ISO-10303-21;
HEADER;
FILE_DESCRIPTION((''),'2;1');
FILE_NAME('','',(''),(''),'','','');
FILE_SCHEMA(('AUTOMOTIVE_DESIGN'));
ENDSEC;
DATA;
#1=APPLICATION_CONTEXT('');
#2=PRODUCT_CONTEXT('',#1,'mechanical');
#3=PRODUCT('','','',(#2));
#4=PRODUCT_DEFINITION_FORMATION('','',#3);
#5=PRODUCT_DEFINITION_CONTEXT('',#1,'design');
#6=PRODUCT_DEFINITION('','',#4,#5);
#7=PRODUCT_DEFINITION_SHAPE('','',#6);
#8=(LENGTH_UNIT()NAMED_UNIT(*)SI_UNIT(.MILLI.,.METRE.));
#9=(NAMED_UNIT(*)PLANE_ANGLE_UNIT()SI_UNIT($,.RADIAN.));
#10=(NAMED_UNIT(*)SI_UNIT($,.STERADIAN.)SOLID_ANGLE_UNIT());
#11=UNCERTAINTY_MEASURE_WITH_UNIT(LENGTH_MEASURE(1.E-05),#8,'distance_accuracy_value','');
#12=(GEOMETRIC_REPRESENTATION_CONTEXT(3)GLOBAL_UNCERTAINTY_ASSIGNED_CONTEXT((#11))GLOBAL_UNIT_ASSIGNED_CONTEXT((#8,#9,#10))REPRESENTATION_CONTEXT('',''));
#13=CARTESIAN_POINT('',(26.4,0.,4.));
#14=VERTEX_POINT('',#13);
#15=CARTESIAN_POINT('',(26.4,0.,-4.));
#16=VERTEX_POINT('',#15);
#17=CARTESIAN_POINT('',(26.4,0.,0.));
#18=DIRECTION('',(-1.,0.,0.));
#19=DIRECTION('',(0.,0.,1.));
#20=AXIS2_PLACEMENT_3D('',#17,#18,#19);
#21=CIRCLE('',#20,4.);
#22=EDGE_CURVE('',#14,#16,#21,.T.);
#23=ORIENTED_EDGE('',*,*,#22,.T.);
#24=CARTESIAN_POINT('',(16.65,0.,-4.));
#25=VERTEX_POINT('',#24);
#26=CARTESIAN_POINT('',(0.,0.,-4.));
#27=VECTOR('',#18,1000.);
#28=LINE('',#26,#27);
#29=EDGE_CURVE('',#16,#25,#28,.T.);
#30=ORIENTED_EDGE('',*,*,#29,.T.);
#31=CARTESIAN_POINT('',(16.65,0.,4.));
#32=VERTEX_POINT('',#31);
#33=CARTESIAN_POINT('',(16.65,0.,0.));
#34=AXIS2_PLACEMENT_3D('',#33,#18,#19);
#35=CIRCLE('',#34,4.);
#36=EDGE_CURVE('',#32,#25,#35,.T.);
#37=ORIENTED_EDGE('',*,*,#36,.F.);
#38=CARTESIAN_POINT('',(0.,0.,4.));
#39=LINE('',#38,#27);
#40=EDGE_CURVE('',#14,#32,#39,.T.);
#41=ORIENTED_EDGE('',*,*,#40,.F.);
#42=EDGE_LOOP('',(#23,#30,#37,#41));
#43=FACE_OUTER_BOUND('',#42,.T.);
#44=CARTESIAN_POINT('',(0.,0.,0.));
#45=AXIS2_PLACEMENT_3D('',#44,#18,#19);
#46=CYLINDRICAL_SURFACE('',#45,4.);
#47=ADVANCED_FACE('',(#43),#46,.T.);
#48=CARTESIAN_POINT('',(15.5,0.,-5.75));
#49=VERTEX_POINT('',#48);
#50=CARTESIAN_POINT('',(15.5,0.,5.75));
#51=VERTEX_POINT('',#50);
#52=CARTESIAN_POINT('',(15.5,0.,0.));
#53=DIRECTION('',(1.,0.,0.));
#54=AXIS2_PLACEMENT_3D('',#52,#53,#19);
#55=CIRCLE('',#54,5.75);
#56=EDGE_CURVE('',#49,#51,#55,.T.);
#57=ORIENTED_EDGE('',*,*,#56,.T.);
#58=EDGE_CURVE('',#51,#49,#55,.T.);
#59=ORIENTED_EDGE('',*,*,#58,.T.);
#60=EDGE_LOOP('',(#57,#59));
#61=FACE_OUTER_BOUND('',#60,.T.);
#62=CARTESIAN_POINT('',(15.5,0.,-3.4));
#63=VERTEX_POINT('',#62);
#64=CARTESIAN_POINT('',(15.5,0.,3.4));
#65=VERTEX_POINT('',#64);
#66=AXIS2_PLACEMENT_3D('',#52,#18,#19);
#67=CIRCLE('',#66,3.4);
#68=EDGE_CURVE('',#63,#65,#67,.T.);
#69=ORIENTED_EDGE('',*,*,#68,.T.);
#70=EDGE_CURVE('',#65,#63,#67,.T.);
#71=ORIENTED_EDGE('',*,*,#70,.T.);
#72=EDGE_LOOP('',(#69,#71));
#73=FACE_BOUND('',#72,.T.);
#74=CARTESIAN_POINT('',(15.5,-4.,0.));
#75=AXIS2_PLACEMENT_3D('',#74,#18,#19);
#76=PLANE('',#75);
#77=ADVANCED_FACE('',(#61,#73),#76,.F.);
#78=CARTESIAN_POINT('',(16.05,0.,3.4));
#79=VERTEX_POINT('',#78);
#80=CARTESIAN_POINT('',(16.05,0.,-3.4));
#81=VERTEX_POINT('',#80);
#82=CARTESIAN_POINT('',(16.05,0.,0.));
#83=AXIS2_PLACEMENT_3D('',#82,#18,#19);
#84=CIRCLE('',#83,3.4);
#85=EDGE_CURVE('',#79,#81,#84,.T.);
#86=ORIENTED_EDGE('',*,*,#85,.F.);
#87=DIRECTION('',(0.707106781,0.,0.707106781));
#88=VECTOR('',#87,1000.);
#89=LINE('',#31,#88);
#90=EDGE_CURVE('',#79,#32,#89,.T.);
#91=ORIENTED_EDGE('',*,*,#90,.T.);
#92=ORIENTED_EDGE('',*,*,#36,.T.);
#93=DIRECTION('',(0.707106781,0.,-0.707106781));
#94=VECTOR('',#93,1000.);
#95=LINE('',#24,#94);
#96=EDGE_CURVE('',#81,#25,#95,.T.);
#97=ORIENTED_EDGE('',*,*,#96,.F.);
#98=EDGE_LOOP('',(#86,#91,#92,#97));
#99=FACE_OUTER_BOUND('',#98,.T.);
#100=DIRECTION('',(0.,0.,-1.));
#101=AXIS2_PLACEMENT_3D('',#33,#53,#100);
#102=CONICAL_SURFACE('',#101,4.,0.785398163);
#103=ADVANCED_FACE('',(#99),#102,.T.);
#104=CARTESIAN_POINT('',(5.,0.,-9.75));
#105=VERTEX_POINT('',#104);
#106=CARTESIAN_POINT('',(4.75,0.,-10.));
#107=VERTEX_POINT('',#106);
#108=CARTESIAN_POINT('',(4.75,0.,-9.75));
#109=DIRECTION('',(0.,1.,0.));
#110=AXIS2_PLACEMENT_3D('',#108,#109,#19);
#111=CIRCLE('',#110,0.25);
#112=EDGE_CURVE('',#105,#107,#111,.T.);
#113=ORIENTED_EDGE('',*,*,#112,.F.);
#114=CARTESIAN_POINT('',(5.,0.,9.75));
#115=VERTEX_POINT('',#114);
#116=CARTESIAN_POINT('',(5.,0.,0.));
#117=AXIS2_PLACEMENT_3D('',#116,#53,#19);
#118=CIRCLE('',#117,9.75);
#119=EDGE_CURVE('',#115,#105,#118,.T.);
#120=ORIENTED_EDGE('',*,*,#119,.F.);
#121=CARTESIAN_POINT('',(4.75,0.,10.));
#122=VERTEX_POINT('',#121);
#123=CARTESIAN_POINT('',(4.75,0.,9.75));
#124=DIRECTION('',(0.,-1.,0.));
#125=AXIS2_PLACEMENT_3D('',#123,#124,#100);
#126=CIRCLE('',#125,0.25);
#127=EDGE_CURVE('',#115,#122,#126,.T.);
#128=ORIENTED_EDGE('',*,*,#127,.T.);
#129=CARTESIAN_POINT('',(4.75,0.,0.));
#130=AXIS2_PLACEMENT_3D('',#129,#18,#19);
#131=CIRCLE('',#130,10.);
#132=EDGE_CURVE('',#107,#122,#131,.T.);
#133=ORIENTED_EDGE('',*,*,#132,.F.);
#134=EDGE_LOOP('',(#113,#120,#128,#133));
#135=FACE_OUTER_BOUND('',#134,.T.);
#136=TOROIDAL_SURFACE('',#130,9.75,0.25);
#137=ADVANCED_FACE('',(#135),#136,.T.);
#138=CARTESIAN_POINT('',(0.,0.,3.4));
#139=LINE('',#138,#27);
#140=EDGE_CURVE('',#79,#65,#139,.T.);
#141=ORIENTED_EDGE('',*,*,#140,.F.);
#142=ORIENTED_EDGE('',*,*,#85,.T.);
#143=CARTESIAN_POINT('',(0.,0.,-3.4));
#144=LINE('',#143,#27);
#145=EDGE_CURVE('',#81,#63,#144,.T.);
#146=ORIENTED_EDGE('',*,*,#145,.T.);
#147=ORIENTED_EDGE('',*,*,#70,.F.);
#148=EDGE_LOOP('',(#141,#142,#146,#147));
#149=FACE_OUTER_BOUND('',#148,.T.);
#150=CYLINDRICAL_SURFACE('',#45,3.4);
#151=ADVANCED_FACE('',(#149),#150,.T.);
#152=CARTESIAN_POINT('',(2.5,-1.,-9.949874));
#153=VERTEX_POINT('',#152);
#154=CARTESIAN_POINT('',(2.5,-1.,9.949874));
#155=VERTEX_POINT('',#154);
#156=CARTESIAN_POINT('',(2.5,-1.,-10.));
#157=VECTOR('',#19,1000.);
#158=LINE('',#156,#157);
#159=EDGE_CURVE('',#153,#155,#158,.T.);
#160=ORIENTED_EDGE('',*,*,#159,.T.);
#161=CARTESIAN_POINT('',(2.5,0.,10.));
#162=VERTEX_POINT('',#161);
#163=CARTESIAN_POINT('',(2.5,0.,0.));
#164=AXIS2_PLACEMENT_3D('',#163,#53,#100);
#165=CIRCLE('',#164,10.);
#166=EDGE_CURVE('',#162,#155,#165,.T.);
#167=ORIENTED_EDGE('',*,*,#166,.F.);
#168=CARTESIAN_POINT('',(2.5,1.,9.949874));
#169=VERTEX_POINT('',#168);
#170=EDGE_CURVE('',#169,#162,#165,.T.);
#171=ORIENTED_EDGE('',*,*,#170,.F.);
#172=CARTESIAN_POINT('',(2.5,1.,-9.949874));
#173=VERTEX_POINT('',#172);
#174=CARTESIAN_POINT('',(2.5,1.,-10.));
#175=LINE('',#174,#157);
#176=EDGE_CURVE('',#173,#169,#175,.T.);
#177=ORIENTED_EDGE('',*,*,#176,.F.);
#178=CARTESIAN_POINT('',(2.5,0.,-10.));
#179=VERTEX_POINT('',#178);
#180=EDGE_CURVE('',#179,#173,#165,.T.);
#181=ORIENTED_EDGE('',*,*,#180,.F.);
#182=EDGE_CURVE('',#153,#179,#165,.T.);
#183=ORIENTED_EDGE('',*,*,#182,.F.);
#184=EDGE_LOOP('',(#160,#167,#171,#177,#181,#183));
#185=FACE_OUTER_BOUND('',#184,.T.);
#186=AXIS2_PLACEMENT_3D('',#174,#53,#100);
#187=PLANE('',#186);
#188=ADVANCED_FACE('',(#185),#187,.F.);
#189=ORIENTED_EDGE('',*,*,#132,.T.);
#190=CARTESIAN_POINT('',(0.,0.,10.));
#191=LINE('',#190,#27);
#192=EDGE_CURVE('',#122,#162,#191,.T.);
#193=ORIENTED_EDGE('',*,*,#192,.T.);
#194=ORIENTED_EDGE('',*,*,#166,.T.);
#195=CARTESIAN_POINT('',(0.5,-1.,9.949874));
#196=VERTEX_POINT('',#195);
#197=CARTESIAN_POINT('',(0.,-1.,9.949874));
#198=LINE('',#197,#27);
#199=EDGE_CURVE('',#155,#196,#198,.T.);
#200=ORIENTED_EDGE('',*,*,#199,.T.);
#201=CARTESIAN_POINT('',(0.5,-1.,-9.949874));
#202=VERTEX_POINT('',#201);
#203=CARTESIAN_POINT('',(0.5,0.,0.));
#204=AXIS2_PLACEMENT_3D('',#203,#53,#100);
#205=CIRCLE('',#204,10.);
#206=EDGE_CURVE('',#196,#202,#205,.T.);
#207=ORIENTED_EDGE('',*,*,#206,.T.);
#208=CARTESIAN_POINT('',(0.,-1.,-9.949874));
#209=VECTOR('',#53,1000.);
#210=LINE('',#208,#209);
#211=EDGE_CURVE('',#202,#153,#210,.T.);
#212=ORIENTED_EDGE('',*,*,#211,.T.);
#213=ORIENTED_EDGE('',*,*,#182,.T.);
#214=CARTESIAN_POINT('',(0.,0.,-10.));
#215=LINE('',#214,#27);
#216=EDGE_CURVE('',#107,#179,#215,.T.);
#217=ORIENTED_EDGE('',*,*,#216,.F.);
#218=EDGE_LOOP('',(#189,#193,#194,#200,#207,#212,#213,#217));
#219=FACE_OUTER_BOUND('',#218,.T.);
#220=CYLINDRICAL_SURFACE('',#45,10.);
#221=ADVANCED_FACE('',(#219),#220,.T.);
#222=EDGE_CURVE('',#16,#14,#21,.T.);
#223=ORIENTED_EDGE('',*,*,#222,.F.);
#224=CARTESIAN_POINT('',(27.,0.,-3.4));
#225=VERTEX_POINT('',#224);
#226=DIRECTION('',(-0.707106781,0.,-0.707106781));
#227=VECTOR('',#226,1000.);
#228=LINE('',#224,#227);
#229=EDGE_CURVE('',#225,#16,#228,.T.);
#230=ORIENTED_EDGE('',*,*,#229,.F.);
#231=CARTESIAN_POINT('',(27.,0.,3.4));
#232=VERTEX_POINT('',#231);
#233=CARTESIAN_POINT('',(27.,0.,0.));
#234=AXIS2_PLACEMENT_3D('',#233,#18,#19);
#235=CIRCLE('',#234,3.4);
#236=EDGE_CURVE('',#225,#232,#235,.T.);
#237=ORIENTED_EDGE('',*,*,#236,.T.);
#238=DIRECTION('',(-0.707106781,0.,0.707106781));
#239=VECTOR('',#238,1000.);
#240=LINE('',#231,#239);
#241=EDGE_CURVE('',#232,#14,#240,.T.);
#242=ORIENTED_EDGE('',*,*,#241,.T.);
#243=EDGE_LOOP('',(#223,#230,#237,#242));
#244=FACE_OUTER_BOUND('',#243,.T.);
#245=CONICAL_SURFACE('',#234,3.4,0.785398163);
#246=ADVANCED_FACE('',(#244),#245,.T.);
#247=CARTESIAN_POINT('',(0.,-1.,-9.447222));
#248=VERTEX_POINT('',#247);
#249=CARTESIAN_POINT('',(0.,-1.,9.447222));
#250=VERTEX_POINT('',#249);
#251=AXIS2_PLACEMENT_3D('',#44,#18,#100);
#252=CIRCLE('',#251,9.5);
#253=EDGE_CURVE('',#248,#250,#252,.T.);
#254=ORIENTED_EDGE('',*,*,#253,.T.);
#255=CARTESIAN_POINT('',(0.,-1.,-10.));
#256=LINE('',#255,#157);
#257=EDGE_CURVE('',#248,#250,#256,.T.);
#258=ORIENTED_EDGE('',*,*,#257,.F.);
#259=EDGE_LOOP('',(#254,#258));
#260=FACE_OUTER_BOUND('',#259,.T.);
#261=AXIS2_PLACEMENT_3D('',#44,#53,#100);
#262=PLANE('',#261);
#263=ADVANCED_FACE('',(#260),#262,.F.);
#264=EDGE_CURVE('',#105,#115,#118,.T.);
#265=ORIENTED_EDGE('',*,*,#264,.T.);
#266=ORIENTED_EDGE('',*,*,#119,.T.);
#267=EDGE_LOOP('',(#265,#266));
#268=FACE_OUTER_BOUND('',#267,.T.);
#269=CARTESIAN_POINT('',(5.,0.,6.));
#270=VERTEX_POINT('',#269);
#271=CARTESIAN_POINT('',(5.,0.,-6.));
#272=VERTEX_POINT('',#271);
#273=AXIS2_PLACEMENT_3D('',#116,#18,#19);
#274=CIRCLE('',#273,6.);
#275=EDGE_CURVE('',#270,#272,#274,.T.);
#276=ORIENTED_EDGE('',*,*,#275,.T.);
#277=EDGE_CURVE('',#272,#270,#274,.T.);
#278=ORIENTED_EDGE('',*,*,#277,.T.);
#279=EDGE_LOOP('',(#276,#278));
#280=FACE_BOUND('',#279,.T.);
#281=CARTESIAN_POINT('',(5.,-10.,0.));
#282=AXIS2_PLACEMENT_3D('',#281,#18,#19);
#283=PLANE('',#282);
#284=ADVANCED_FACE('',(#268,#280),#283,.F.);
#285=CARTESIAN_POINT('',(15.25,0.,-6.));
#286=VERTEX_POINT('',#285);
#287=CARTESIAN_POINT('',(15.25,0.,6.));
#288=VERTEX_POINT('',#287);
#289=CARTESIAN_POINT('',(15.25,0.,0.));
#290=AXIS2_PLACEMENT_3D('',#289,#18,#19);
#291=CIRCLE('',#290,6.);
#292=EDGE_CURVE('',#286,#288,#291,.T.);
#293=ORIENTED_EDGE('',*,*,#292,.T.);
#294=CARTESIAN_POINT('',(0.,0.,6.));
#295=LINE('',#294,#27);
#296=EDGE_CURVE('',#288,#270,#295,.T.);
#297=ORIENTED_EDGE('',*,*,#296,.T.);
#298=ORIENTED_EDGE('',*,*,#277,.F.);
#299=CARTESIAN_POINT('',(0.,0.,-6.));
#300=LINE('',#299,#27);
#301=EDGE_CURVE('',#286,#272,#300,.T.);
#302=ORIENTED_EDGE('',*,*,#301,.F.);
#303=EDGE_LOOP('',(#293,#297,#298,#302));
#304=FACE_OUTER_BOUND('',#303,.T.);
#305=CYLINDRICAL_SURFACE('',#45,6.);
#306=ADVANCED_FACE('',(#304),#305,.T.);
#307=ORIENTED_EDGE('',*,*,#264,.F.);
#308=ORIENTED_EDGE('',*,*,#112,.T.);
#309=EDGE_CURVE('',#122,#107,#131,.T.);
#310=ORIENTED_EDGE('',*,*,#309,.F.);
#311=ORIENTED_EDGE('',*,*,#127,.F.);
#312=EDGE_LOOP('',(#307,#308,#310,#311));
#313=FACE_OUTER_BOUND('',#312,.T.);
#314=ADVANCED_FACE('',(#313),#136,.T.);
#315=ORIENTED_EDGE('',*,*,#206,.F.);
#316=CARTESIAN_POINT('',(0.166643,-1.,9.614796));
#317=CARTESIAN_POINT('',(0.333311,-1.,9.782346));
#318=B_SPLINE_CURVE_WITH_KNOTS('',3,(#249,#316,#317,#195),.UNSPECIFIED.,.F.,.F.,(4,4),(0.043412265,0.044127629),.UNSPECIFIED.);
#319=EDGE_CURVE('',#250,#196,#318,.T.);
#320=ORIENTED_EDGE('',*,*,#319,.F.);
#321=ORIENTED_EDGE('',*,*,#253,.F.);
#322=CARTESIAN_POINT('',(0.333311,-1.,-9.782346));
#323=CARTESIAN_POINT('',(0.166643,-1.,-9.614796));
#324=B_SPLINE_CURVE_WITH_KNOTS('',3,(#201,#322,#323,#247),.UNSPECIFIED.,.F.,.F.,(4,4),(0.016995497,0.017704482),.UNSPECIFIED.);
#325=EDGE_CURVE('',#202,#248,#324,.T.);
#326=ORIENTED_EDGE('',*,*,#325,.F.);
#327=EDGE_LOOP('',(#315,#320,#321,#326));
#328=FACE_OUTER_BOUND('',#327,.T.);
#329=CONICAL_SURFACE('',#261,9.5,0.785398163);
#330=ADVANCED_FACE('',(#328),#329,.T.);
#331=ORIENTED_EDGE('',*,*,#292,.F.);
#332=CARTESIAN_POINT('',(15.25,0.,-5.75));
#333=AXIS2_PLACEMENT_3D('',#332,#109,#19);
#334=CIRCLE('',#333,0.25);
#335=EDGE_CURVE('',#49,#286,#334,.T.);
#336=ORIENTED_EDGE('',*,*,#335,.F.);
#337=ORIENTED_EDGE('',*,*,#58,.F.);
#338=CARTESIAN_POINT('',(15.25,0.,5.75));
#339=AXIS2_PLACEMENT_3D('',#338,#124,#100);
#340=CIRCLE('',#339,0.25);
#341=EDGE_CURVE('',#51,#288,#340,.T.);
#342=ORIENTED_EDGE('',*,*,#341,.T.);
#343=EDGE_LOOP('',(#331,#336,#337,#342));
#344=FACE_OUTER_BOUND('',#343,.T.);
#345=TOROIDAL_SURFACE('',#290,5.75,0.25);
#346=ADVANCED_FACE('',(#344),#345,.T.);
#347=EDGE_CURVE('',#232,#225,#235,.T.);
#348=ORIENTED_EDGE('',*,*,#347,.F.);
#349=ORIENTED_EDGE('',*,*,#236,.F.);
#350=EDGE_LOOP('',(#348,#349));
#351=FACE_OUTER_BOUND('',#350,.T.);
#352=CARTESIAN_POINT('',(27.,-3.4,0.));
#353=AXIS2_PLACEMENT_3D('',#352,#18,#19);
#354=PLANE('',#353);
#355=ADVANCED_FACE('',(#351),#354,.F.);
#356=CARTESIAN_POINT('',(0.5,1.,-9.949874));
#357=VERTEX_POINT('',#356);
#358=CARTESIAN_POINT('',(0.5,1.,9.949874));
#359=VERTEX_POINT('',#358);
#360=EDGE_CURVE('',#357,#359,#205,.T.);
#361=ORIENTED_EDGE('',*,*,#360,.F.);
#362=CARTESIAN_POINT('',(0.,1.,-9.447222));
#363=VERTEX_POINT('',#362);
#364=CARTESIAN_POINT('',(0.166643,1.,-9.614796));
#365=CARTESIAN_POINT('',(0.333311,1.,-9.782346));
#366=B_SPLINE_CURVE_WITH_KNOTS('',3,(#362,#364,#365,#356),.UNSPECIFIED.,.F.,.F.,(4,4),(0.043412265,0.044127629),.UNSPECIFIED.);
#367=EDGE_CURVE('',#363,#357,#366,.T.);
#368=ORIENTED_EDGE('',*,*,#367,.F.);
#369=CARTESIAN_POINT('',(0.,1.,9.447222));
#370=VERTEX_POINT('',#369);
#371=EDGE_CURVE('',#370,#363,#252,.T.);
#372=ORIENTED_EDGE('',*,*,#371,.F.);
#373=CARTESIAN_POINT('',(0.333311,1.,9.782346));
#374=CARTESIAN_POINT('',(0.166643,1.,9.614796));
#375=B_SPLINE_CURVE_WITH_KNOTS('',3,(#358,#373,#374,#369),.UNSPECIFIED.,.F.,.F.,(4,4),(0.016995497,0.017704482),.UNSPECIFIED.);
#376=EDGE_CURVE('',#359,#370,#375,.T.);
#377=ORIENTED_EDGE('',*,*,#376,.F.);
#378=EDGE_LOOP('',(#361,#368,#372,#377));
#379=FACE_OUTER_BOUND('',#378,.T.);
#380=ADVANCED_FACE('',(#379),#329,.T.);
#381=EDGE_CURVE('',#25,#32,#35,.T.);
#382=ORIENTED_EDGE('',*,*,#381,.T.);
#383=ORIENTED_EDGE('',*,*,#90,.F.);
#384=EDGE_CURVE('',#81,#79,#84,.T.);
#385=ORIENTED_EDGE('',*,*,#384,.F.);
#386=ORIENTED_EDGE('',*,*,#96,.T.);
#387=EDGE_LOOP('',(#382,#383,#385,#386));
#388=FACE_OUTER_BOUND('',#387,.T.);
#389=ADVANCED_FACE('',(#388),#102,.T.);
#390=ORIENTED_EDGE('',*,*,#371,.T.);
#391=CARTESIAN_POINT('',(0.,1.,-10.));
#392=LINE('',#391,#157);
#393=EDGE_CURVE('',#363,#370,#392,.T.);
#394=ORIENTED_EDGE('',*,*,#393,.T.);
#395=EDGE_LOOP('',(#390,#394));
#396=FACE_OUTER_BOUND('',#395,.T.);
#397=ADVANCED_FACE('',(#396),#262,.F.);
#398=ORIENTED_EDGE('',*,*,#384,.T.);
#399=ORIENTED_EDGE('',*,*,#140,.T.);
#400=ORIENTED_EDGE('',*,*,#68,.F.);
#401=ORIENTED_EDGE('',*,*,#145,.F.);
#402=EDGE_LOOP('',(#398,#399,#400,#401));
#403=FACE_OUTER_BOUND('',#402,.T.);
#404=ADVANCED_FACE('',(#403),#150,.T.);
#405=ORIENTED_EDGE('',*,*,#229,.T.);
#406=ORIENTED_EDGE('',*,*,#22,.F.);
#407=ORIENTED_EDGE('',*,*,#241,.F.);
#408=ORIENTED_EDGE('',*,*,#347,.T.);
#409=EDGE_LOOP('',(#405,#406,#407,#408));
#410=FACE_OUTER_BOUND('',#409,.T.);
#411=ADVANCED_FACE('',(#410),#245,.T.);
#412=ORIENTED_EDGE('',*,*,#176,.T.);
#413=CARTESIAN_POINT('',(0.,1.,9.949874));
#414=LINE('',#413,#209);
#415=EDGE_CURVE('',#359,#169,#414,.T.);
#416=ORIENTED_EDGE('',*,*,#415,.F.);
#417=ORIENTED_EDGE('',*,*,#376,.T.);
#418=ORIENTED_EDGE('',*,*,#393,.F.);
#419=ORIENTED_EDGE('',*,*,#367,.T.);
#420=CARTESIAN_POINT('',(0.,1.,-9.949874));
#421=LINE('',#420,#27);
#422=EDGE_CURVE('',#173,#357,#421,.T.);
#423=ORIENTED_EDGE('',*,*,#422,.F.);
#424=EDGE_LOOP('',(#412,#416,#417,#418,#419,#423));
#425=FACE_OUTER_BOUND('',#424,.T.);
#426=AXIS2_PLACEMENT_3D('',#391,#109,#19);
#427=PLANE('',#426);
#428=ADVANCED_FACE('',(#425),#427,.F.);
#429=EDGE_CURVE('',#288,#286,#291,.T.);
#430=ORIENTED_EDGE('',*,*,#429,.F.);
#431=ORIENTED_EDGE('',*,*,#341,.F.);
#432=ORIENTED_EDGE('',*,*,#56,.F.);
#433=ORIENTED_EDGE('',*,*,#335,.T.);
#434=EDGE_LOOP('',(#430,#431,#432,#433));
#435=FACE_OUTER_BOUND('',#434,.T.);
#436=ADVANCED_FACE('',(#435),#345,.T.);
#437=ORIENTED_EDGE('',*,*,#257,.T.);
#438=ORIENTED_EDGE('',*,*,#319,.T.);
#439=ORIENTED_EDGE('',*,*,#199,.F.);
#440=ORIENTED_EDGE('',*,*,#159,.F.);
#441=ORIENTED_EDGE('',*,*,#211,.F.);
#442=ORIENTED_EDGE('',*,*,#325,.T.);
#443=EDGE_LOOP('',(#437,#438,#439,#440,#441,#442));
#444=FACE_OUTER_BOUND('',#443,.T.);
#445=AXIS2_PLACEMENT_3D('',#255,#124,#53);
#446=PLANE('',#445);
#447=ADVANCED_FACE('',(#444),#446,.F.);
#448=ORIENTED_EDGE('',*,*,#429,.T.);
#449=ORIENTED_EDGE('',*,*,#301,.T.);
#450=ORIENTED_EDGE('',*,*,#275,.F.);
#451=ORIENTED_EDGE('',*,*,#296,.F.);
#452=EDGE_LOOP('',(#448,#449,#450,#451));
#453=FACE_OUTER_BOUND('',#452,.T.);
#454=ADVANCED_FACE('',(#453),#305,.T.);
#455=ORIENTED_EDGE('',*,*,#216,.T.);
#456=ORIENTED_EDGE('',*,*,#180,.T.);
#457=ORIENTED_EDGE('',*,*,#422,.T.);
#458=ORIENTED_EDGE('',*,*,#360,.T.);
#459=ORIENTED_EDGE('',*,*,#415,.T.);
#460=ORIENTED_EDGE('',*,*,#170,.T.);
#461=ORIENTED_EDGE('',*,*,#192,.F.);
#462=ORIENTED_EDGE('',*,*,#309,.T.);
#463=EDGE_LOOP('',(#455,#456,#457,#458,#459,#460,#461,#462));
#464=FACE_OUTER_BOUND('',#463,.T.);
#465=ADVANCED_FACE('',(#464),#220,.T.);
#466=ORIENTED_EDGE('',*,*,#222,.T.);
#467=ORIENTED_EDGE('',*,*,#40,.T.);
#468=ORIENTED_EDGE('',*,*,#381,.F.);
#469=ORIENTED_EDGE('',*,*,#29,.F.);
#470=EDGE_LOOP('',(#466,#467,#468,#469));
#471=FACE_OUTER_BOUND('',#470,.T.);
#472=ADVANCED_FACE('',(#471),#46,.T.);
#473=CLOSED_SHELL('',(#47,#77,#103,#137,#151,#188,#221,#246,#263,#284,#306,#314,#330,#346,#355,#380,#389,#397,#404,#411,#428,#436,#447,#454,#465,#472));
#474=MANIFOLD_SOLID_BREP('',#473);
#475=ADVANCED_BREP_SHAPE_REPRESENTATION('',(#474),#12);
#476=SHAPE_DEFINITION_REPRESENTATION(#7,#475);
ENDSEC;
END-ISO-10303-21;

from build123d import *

# Parameters (mm, degrees)
CHAMFER1_SIZE           = 0.5
CUT_EXTRUDE1_DEPTH      = 31.479501308
CUT_EXTRUDE1_DEPTH_BACK = 31.479501308
SKETCH3_W               = 2.5
SKETCH3_H               = 2
FILLET1_R               = 0.25


with BuildPart() as part:
    # Sketch2 → Revolve1 (revolve)
    with BuildSketch(Plane.XY, mode=Mode.PRIVATE) as revolve1_sk:
        Polygon((0, 0), (0, 10), (5, 10), (5, 6), (15.5, 6), (15.5, 4), (15.5, 3.4), (16.05, 3.4), (16.65, 4), (26.4, 4), (27, 3.4), (27, 0), align=None)
    revolve(revolve1_sk.sketch.rotate(Axis((0, 0, 0), (1, 0, 0)), 90), axis=Axis((0, 0, 0), (1, 0, 0)))

    # Chamfer1
    chamfer1_edges = [part.edges().sort_by_distance(p)[0] for p in [
        (0, 0, -10),
    ]]
    chamfer(chamfer1_edges, length=CHAMFER1_SIZE)

    # Sketch3 → Cut-Extrude1 (cut, two sides: drawn at the far end of the back side and taken through both)
    with BuildSketch(Plane.XY.offset(-CUT_EXTRUDE1_DEPTH_BACK)):
        with Locations((1.25, 0)):
            Rectangle(SKETCH3_W, SKETCH3_H)
    extrude(amount=CUT_EXTRUDE1_DEPTH + CUT_EXTRUDE1_DEPTH_BACK, mode=Mode.SUBTRACT)

    # Fillet1
    fillet1_edges = [part.edges().sort_by_distance(p)[0] for p in [
        (15.5, 0, -6),
        (5, 0, -10),
    ]]
    fillet(fillet1_edges, radius=FILLET1_R)


solid = part.part
